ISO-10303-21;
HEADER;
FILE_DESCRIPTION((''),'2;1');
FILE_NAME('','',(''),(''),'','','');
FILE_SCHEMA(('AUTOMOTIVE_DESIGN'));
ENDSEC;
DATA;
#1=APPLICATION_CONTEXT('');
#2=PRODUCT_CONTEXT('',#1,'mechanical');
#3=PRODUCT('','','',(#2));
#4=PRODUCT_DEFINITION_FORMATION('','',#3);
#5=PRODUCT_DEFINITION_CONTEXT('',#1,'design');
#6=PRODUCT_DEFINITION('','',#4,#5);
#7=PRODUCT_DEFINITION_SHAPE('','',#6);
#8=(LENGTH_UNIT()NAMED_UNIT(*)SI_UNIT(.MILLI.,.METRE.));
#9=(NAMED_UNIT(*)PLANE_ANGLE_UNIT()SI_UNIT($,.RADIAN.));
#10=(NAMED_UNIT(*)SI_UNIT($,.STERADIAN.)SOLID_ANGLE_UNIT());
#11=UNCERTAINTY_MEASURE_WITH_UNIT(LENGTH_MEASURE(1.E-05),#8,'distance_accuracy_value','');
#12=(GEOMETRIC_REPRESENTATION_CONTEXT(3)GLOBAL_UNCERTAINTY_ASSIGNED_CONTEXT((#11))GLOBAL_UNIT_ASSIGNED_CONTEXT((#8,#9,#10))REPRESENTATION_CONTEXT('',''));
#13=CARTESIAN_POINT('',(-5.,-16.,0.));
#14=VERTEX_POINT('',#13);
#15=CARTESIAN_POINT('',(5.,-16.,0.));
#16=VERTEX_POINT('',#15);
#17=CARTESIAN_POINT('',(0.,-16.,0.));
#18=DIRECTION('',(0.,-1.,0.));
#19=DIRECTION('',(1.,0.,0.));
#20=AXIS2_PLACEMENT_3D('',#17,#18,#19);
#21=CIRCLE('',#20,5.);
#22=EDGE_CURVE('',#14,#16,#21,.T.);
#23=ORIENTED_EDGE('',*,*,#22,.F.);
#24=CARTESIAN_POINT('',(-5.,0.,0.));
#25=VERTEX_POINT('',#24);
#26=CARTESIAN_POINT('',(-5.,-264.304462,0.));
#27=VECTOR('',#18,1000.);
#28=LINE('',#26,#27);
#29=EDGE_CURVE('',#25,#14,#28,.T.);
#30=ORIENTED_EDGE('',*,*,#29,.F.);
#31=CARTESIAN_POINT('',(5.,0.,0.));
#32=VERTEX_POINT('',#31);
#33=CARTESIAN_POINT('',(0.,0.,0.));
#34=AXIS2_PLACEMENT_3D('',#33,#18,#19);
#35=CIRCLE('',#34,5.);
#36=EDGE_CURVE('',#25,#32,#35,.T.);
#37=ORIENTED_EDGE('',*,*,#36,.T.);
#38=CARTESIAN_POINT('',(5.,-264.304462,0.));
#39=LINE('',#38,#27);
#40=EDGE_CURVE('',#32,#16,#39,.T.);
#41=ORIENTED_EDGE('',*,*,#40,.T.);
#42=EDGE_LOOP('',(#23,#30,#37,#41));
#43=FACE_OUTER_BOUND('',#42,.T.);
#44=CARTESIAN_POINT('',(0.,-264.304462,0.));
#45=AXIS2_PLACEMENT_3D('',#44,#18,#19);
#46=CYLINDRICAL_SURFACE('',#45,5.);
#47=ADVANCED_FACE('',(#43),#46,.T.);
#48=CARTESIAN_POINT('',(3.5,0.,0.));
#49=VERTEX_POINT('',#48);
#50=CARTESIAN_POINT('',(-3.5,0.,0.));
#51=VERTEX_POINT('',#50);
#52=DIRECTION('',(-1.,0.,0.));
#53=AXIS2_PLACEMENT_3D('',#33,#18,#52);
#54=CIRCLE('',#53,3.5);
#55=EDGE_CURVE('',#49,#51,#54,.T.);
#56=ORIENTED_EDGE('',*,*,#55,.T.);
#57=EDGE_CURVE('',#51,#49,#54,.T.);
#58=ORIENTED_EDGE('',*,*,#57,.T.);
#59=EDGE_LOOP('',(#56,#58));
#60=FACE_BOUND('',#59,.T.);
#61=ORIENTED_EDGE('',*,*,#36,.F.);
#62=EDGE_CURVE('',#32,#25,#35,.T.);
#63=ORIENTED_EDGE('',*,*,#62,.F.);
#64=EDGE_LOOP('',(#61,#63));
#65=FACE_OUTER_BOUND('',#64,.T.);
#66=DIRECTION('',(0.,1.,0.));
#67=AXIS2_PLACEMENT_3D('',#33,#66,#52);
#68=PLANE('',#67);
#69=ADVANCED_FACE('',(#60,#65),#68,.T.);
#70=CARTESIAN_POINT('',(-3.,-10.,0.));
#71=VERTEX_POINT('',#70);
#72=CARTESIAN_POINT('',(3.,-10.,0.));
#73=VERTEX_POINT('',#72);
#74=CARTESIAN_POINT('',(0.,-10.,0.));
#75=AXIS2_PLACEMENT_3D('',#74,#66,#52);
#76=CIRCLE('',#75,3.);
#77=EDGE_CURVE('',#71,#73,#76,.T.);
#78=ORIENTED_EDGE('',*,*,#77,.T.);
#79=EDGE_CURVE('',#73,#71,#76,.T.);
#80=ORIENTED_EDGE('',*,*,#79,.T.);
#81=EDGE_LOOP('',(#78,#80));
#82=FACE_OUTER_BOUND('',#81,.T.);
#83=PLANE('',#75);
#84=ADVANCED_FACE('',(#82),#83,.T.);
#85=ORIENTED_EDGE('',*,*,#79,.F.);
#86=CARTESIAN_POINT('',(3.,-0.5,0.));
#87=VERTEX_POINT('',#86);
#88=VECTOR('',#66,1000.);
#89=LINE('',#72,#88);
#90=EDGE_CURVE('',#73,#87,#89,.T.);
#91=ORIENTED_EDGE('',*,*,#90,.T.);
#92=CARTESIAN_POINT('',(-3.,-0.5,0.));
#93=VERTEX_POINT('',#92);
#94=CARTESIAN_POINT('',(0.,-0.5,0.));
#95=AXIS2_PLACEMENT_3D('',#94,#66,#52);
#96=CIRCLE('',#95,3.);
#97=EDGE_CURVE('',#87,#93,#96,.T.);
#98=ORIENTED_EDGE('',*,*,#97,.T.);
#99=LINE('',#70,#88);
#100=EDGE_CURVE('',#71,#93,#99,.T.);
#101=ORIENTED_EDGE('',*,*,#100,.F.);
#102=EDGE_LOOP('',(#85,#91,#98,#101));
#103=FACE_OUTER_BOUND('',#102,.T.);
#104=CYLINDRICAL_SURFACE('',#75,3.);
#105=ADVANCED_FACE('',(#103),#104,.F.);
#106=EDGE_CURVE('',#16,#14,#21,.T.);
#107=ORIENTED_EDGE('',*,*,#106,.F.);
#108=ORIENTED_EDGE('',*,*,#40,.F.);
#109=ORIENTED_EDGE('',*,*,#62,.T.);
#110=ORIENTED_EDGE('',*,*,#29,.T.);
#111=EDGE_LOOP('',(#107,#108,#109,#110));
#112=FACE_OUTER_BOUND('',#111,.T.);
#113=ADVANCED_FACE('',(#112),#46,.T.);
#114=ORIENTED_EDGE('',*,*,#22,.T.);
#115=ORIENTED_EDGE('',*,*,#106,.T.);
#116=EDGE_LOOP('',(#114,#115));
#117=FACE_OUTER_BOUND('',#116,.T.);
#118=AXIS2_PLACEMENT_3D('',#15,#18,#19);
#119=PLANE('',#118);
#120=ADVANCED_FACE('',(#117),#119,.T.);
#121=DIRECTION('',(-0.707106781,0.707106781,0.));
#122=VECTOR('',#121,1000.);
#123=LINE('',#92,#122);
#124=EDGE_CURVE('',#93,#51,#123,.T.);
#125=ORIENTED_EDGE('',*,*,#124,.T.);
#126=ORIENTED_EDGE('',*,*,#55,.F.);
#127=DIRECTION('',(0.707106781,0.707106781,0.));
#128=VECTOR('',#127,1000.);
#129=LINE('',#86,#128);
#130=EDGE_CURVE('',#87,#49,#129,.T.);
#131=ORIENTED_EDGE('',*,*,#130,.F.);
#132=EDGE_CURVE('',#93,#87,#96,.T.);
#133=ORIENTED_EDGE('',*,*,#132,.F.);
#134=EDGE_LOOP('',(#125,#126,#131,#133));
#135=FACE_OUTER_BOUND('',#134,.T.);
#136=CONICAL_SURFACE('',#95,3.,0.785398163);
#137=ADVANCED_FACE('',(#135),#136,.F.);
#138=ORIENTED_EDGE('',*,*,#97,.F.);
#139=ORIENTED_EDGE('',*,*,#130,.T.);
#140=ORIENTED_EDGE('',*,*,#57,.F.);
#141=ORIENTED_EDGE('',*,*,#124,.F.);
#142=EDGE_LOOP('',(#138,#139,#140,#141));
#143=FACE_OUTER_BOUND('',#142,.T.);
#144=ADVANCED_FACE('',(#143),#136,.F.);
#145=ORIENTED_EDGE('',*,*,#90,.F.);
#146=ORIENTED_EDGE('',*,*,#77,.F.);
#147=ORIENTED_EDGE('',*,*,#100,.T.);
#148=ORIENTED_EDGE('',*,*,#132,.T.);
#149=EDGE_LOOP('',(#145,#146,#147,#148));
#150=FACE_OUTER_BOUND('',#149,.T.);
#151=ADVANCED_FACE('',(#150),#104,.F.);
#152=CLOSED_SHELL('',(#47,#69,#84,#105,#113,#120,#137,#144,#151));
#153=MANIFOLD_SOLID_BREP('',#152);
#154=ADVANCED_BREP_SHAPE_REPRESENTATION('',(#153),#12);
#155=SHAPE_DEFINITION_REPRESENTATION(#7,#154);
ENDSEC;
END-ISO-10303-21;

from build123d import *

# Parameters (mm, degrees)
SKETCH1_W          = 5
SKETCH1_H          = 16
SKETCH2_R          = 3
CUT_EXTRUDE1_DEPTH = 10
CHAMFER1_SIZE      = 0.5


with BuildPart() as part:
    # Sketch1 → Revolve1 (revolve)
    with BuildSketch(Plane.XY):
        with Locations((2.5, -8)):
            Rectangle(SKETCH1_W, SKETCH1_H)
    revolve(axis=Axis((0, -264.304461942, 0), (0, 1, 0)))

    # Sketch2 → Cut-Extrude1 (cut)
    with BuildSketch(Plane(origin=(0, 0, 0), x_dir=(1, 0, 0), z_dir=(0, 1, 0))):
        with Locations(Location((0, 0, 0), (0, 0, 180))):
            Circle(SKETCH2_R)
    extrude(amount=-CUT_EXTRUDE1_DEPTH, mode=Mode.SUBTRACT)

    # Chamfer1
    chamfer1_edges = [part.edges().sort_by_distance(p)[0] for p in [
        (3, 0, 0),
    ]]
    chamfer(chamfer1_edges, length=CHAMFER1_SIZE)


solid = part.part
